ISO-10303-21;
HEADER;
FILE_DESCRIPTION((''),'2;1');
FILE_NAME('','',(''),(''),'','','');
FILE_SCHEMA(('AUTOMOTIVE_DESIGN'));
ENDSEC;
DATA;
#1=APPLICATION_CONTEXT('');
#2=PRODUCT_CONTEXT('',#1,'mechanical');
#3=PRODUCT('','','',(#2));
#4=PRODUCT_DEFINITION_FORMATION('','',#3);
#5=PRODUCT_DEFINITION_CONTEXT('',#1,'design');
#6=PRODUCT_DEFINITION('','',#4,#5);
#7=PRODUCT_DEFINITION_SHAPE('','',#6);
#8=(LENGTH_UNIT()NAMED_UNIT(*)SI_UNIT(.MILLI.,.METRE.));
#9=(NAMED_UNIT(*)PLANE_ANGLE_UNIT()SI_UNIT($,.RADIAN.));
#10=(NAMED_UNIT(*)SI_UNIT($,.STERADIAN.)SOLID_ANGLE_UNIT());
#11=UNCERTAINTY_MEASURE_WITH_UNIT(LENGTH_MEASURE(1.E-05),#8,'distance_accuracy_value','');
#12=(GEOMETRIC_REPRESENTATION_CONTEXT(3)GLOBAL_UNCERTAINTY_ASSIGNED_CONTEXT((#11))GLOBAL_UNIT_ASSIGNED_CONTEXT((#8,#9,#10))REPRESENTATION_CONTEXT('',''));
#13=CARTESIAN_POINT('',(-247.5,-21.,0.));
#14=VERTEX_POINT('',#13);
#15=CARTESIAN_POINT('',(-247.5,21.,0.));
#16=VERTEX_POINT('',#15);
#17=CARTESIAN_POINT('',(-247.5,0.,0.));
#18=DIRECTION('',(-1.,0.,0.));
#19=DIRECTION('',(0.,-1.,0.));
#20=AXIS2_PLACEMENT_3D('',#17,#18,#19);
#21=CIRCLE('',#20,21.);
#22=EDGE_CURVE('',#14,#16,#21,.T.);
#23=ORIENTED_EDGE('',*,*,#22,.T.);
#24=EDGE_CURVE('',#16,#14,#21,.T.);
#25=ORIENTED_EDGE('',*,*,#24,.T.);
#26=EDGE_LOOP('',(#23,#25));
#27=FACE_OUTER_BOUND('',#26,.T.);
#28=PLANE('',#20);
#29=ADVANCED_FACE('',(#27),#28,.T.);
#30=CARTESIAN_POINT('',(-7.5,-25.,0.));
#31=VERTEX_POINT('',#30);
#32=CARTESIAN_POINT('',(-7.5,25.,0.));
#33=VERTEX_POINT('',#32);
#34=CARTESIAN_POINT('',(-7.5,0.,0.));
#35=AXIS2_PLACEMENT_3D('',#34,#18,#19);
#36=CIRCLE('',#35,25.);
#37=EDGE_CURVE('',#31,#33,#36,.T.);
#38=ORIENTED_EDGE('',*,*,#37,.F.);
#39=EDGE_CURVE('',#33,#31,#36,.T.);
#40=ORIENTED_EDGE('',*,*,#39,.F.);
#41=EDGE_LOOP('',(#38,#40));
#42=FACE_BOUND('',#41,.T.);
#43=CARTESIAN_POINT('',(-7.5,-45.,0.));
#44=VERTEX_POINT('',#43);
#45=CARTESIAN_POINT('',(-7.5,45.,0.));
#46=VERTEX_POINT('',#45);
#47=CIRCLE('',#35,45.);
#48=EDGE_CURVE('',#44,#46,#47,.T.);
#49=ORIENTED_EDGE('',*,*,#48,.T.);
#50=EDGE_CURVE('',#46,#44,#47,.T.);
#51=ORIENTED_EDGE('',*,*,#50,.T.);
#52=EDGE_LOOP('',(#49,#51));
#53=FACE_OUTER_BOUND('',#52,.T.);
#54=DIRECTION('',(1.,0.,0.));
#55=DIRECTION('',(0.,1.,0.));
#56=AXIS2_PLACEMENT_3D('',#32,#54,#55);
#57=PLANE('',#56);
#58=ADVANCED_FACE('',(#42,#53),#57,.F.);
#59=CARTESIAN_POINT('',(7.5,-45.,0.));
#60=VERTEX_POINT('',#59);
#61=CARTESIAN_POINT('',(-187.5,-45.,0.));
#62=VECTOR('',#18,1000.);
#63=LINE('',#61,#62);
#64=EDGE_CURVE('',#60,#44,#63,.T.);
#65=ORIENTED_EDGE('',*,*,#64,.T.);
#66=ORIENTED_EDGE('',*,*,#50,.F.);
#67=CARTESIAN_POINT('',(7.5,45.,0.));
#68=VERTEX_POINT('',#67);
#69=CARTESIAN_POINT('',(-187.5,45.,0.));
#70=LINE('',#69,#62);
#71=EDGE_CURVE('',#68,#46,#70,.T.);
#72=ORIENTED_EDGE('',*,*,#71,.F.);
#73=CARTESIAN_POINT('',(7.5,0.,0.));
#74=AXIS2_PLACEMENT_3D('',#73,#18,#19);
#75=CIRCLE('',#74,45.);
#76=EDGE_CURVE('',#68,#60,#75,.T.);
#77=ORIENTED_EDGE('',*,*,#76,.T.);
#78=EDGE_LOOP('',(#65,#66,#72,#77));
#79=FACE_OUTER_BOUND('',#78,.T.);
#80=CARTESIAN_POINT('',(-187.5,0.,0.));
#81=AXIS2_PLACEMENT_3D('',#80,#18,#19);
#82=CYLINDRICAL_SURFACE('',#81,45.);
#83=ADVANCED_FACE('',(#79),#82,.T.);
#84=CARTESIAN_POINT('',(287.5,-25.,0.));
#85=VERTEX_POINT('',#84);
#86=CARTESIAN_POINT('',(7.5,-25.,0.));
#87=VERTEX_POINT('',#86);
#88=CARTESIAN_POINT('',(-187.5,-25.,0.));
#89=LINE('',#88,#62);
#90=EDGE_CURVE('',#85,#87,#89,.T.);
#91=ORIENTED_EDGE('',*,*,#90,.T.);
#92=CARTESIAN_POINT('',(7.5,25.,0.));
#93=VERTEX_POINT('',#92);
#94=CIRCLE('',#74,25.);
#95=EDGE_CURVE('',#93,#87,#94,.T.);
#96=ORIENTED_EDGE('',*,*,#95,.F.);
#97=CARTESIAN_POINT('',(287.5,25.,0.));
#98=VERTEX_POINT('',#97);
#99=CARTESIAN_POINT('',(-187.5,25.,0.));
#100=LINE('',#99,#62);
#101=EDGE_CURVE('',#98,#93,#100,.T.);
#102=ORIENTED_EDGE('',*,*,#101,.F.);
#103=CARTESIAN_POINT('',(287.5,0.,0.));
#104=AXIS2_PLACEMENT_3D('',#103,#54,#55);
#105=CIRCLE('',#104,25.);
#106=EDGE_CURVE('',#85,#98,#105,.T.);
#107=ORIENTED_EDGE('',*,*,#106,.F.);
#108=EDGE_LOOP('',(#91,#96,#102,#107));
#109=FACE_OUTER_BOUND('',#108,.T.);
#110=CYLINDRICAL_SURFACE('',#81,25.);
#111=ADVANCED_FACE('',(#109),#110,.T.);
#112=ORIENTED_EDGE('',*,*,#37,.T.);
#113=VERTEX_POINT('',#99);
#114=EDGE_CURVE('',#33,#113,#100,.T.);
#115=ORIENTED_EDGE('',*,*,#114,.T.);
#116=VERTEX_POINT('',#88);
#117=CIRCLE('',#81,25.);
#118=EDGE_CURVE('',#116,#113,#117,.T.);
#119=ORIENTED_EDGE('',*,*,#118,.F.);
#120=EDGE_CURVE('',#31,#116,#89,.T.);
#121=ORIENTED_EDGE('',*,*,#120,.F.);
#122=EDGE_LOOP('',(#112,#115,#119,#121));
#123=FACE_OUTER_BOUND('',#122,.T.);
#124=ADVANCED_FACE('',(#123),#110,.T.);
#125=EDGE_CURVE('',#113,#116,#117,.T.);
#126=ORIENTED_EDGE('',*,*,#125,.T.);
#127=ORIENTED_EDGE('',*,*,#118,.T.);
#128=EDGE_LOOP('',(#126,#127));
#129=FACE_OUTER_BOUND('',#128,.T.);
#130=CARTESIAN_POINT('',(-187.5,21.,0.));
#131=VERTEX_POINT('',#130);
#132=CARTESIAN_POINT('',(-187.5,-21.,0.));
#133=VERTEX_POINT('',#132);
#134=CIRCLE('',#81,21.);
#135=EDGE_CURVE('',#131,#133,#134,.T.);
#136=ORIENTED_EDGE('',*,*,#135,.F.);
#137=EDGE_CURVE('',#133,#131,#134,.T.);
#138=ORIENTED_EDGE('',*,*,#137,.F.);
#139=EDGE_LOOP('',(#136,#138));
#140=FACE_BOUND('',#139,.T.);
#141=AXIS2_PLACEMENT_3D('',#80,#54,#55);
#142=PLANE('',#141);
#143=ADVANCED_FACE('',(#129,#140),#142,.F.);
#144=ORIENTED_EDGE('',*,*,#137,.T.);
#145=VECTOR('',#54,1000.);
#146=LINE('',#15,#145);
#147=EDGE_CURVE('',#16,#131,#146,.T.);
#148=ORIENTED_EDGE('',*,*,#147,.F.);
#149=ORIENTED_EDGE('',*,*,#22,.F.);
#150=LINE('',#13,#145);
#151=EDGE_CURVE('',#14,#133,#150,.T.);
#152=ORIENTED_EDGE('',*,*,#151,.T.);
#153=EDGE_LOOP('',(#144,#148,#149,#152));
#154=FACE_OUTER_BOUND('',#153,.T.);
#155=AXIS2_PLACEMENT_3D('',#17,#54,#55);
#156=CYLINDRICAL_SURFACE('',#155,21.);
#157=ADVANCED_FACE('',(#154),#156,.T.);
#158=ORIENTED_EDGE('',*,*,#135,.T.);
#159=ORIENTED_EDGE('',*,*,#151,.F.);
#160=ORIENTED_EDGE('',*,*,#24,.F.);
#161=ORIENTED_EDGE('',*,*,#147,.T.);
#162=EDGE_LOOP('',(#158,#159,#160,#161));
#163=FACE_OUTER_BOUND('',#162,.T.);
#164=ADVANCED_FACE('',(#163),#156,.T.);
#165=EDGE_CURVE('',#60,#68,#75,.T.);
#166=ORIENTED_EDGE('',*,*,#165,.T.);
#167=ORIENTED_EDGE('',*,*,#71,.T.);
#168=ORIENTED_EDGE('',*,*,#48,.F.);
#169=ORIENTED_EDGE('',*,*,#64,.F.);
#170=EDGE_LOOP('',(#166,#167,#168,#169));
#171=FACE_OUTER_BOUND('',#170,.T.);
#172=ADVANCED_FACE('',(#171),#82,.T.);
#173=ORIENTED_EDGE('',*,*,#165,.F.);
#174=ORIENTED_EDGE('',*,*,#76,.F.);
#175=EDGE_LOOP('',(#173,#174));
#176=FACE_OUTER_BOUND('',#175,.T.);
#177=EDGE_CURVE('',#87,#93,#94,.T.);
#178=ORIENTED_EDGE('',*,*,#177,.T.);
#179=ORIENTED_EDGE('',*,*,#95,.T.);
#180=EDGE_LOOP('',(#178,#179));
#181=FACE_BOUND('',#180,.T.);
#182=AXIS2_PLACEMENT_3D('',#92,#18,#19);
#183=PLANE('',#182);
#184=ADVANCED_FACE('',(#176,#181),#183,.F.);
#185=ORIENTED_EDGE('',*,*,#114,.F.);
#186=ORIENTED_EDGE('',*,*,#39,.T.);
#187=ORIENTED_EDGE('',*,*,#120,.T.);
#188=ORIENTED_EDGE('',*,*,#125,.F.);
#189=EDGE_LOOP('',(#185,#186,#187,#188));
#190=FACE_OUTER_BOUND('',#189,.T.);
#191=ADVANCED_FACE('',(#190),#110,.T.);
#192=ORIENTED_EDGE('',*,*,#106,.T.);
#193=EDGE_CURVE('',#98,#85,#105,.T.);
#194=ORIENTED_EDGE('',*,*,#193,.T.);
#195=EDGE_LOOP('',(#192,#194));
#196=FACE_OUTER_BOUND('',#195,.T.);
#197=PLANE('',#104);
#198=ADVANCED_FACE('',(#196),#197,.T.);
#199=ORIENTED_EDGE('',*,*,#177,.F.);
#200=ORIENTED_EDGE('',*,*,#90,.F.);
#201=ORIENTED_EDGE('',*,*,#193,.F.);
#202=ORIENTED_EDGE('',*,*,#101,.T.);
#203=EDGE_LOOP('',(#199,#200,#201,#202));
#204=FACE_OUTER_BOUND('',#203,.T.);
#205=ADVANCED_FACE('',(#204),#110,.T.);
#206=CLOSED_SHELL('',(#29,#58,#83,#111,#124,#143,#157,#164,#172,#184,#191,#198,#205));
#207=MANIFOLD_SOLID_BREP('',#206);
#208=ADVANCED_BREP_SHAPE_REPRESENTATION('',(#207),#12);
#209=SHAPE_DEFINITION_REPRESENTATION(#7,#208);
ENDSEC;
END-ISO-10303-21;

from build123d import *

# Parameters (mm, degrees)
BOSS_EXTRUDE_START   = 100
SKETCH_2_R           = 25
BOSS_EXTRUDE_1_DEPTH = 100
SKETCH_3_R           = 21
BOSS_EXTRUDE_2_DEPTH = 60


with BuildPart() as part:
    # Sketch 1 → Revolve 1 (revolve)
    with BuildSketch(Plane.XY, mode=Mode.PRIVATE) as revolve_1_sk:
        Polygon((-187.5, 0), (-187.5, 25), (-7.5, 25), (-7.5, 45), (7.5, 45), (7.5, 25), (187.5, 25), (187.5, 0), align=None)
    revolve(revolve_1_sk.sketch.rotate(Axis((-187.5, 0, 0), (1, 0, 0)), 180), axis=Axis((-187.5, 0, 0), (1, 0, 0)))

    # Sketch 2 → Boss-Extrude 1 (add)
    with BuildSketch(Plane(origin=(187.5, 0, 0), x_dir=(0, 0, -1), z_dir=(1, 0, 0)).offset(BOSS_EXTRUDE_START)):
        with Locations(Location((0, 0, 0), (0, 0, 270))):
            Circle(SKETCH_2_R)
    extrude(amount=-BOSS_EXTRUDE_1_DEPTH)

    # Sketch 3 → Boss-Extrude 2 (add)
    with BuildSketch(Plane.ZY.offset(187.5)):
        with Locations(Location((0, 0, 0), (0, 0, 270))):
            Circle(SKETCH_3_R)
    extrude(amount=BOSS_EXTRUDE_2_DEPTH)


solid = part.part
